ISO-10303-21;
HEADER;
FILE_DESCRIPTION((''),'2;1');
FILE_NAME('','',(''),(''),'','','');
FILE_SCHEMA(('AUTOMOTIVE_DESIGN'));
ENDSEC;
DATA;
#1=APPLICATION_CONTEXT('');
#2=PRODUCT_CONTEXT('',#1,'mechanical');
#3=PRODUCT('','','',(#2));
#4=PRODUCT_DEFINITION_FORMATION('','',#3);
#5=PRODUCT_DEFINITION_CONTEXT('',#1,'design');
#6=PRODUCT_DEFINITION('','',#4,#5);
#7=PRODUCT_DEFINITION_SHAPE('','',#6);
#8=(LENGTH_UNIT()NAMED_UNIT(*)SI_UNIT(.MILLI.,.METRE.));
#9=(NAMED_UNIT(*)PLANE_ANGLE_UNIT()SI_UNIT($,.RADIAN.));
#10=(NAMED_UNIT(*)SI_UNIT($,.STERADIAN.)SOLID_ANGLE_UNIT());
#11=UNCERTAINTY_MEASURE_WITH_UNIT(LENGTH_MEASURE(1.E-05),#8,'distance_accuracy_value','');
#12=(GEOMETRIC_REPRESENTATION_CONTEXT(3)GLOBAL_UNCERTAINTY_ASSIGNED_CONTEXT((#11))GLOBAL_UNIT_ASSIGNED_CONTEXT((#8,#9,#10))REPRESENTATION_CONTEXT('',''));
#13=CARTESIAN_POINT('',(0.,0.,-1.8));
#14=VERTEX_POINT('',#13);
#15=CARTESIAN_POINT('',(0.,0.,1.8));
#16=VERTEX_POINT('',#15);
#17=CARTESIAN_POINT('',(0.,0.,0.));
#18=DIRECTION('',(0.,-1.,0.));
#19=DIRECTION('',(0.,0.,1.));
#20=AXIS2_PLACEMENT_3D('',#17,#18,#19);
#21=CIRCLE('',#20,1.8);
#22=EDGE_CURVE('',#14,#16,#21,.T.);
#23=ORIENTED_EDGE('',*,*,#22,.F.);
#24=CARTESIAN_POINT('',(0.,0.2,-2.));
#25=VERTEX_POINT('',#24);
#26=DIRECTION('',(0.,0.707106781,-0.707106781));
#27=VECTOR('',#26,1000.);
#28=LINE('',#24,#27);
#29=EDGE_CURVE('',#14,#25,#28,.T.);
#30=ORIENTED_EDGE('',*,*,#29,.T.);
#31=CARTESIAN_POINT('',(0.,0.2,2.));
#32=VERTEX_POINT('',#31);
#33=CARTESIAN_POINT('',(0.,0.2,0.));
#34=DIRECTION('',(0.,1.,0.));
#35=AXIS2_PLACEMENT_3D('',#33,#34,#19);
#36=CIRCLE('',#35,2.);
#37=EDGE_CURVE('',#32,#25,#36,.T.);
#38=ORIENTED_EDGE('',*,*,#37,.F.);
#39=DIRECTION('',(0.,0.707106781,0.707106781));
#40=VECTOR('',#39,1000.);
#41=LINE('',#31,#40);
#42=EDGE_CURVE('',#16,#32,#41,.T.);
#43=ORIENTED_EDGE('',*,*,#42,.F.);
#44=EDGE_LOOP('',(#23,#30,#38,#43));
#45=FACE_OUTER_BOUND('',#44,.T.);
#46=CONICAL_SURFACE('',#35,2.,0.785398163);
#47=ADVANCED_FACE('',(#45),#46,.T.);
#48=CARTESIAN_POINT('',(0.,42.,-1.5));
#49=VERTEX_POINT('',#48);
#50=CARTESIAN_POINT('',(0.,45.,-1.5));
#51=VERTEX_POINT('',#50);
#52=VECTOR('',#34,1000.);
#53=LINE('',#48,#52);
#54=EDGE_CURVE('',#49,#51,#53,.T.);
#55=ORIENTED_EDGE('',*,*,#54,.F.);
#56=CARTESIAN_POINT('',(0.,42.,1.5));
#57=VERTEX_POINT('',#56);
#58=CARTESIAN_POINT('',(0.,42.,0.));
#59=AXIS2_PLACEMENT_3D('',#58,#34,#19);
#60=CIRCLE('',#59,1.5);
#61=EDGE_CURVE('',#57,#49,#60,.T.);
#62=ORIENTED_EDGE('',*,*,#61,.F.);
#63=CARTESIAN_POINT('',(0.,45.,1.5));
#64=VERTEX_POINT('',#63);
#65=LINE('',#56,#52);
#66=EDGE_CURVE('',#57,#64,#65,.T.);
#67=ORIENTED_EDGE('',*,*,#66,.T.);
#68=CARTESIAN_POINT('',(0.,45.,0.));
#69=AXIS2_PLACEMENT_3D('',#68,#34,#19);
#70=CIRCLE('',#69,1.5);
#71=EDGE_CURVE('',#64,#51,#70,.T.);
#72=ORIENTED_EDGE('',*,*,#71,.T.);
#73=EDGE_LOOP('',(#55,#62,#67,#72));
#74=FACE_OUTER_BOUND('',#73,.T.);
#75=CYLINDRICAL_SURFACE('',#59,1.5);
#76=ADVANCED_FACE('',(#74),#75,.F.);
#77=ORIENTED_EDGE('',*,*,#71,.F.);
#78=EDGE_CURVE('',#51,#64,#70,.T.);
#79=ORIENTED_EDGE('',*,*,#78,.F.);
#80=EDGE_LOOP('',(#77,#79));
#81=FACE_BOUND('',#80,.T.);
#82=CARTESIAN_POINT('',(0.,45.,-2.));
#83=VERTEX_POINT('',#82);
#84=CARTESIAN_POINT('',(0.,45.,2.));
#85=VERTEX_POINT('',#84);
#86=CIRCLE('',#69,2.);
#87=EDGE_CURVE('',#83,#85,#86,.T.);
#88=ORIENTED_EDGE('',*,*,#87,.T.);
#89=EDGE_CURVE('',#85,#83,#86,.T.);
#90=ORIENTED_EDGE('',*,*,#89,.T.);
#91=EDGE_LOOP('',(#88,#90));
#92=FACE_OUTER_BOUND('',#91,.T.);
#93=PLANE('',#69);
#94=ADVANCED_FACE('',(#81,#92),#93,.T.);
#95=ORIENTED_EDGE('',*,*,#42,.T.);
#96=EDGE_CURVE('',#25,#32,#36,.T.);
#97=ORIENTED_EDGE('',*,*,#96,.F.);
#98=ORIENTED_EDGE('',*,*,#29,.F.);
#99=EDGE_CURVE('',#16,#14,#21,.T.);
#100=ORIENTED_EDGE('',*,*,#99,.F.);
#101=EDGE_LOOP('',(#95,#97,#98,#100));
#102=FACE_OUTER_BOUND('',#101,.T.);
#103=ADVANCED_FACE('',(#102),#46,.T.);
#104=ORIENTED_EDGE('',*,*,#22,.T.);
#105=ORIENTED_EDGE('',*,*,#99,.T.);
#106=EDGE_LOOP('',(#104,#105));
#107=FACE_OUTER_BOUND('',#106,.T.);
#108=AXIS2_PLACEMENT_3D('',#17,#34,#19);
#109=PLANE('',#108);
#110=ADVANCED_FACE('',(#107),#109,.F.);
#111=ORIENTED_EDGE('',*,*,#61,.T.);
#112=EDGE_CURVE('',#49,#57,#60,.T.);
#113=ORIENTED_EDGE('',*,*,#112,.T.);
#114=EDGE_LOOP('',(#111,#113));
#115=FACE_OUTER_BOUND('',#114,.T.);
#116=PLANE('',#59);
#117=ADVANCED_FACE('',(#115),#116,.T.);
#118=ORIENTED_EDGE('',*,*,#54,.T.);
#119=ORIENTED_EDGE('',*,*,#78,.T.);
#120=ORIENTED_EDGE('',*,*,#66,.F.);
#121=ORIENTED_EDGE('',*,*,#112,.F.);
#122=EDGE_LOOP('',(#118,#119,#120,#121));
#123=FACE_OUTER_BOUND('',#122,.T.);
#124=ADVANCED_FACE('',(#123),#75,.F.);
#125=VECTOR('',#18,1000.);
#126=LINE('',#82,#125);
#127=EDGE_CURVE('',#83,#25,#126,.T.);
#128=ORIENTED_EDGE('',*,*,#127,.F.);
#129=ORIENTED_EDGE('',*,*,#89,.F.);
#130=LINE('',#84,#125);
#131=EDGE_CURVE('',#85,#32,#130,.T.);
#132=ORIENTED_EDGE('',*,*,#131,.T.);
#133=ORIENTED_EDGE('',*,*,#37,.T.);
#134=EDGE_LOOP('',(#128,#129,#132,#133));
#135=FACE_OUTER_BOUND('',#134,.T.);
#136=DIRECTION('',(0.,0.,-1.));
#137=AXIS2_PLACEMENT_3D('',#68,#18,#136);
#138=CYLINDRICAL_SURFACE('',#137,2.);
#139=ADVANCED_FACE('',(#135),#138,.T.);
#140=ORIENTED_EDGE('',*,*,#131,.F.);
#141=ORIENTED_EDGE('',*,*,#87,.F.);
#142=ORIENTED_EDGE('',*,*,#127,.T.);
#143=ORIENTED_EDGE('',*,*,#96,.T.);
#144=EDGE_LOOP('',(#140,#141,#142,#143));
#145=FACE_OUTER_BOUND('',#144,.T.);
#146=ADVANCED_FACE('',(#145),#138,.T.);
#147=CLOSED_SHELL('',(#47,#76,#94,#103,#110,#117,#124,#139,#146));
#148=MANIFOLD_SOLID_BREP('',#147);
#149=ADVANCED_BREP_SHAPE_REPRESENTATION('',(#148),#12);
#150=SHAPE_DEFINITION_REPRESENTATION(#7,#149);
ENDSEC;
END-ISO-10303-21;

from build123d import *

# Parameters (mm, degrees)
SKETCH1_R           = 2
BOSS_EXTRUDE1_DEPTH = 45
CHAMFER1_SIZE       = 0.2
SKETCH3_R           = 1.5
CUT_EXTRUDE1_DEPTH  = 3


with BuildPart() as part:
    # Sketch1 → Boss-Extrude1 (new body)
    with BuildSketch(Plane(origin=(0, 0, 0), x_dir=(1, 0, 0), z_dir=(0, 1, 0))):
        with Locations(Location((0, 0, 0), (0, 0, 90))):
            Circle(SKETCH1_R)
    extrude(amount=BOSS_EXTRUDE1_DEPTH)

    # Chamfer1
    chamfer1_edges = [part.edges().sort_by_distance(p)[0] for p in [
        (0, 0, 2),
    ]]
    chamfer(chamfer1_edges, length=CHAMFER1_SIZE)

    # Sketch3 → Cut-Extrude1 (cut)
    with BuildSketch(Plane(origin=(0, 45, 0), x_dir=(1, 0, 0), z_dir=(0, 1, 0))):
        with Locations(Location((0, 0, 0), (0, 0, 270))):
            Circle(SKETCH3_R)
    extrude(amount=-CUT_EXTRUDE1_DEPTH, mode=Mode.SUBTRACT)


solid = part.part
